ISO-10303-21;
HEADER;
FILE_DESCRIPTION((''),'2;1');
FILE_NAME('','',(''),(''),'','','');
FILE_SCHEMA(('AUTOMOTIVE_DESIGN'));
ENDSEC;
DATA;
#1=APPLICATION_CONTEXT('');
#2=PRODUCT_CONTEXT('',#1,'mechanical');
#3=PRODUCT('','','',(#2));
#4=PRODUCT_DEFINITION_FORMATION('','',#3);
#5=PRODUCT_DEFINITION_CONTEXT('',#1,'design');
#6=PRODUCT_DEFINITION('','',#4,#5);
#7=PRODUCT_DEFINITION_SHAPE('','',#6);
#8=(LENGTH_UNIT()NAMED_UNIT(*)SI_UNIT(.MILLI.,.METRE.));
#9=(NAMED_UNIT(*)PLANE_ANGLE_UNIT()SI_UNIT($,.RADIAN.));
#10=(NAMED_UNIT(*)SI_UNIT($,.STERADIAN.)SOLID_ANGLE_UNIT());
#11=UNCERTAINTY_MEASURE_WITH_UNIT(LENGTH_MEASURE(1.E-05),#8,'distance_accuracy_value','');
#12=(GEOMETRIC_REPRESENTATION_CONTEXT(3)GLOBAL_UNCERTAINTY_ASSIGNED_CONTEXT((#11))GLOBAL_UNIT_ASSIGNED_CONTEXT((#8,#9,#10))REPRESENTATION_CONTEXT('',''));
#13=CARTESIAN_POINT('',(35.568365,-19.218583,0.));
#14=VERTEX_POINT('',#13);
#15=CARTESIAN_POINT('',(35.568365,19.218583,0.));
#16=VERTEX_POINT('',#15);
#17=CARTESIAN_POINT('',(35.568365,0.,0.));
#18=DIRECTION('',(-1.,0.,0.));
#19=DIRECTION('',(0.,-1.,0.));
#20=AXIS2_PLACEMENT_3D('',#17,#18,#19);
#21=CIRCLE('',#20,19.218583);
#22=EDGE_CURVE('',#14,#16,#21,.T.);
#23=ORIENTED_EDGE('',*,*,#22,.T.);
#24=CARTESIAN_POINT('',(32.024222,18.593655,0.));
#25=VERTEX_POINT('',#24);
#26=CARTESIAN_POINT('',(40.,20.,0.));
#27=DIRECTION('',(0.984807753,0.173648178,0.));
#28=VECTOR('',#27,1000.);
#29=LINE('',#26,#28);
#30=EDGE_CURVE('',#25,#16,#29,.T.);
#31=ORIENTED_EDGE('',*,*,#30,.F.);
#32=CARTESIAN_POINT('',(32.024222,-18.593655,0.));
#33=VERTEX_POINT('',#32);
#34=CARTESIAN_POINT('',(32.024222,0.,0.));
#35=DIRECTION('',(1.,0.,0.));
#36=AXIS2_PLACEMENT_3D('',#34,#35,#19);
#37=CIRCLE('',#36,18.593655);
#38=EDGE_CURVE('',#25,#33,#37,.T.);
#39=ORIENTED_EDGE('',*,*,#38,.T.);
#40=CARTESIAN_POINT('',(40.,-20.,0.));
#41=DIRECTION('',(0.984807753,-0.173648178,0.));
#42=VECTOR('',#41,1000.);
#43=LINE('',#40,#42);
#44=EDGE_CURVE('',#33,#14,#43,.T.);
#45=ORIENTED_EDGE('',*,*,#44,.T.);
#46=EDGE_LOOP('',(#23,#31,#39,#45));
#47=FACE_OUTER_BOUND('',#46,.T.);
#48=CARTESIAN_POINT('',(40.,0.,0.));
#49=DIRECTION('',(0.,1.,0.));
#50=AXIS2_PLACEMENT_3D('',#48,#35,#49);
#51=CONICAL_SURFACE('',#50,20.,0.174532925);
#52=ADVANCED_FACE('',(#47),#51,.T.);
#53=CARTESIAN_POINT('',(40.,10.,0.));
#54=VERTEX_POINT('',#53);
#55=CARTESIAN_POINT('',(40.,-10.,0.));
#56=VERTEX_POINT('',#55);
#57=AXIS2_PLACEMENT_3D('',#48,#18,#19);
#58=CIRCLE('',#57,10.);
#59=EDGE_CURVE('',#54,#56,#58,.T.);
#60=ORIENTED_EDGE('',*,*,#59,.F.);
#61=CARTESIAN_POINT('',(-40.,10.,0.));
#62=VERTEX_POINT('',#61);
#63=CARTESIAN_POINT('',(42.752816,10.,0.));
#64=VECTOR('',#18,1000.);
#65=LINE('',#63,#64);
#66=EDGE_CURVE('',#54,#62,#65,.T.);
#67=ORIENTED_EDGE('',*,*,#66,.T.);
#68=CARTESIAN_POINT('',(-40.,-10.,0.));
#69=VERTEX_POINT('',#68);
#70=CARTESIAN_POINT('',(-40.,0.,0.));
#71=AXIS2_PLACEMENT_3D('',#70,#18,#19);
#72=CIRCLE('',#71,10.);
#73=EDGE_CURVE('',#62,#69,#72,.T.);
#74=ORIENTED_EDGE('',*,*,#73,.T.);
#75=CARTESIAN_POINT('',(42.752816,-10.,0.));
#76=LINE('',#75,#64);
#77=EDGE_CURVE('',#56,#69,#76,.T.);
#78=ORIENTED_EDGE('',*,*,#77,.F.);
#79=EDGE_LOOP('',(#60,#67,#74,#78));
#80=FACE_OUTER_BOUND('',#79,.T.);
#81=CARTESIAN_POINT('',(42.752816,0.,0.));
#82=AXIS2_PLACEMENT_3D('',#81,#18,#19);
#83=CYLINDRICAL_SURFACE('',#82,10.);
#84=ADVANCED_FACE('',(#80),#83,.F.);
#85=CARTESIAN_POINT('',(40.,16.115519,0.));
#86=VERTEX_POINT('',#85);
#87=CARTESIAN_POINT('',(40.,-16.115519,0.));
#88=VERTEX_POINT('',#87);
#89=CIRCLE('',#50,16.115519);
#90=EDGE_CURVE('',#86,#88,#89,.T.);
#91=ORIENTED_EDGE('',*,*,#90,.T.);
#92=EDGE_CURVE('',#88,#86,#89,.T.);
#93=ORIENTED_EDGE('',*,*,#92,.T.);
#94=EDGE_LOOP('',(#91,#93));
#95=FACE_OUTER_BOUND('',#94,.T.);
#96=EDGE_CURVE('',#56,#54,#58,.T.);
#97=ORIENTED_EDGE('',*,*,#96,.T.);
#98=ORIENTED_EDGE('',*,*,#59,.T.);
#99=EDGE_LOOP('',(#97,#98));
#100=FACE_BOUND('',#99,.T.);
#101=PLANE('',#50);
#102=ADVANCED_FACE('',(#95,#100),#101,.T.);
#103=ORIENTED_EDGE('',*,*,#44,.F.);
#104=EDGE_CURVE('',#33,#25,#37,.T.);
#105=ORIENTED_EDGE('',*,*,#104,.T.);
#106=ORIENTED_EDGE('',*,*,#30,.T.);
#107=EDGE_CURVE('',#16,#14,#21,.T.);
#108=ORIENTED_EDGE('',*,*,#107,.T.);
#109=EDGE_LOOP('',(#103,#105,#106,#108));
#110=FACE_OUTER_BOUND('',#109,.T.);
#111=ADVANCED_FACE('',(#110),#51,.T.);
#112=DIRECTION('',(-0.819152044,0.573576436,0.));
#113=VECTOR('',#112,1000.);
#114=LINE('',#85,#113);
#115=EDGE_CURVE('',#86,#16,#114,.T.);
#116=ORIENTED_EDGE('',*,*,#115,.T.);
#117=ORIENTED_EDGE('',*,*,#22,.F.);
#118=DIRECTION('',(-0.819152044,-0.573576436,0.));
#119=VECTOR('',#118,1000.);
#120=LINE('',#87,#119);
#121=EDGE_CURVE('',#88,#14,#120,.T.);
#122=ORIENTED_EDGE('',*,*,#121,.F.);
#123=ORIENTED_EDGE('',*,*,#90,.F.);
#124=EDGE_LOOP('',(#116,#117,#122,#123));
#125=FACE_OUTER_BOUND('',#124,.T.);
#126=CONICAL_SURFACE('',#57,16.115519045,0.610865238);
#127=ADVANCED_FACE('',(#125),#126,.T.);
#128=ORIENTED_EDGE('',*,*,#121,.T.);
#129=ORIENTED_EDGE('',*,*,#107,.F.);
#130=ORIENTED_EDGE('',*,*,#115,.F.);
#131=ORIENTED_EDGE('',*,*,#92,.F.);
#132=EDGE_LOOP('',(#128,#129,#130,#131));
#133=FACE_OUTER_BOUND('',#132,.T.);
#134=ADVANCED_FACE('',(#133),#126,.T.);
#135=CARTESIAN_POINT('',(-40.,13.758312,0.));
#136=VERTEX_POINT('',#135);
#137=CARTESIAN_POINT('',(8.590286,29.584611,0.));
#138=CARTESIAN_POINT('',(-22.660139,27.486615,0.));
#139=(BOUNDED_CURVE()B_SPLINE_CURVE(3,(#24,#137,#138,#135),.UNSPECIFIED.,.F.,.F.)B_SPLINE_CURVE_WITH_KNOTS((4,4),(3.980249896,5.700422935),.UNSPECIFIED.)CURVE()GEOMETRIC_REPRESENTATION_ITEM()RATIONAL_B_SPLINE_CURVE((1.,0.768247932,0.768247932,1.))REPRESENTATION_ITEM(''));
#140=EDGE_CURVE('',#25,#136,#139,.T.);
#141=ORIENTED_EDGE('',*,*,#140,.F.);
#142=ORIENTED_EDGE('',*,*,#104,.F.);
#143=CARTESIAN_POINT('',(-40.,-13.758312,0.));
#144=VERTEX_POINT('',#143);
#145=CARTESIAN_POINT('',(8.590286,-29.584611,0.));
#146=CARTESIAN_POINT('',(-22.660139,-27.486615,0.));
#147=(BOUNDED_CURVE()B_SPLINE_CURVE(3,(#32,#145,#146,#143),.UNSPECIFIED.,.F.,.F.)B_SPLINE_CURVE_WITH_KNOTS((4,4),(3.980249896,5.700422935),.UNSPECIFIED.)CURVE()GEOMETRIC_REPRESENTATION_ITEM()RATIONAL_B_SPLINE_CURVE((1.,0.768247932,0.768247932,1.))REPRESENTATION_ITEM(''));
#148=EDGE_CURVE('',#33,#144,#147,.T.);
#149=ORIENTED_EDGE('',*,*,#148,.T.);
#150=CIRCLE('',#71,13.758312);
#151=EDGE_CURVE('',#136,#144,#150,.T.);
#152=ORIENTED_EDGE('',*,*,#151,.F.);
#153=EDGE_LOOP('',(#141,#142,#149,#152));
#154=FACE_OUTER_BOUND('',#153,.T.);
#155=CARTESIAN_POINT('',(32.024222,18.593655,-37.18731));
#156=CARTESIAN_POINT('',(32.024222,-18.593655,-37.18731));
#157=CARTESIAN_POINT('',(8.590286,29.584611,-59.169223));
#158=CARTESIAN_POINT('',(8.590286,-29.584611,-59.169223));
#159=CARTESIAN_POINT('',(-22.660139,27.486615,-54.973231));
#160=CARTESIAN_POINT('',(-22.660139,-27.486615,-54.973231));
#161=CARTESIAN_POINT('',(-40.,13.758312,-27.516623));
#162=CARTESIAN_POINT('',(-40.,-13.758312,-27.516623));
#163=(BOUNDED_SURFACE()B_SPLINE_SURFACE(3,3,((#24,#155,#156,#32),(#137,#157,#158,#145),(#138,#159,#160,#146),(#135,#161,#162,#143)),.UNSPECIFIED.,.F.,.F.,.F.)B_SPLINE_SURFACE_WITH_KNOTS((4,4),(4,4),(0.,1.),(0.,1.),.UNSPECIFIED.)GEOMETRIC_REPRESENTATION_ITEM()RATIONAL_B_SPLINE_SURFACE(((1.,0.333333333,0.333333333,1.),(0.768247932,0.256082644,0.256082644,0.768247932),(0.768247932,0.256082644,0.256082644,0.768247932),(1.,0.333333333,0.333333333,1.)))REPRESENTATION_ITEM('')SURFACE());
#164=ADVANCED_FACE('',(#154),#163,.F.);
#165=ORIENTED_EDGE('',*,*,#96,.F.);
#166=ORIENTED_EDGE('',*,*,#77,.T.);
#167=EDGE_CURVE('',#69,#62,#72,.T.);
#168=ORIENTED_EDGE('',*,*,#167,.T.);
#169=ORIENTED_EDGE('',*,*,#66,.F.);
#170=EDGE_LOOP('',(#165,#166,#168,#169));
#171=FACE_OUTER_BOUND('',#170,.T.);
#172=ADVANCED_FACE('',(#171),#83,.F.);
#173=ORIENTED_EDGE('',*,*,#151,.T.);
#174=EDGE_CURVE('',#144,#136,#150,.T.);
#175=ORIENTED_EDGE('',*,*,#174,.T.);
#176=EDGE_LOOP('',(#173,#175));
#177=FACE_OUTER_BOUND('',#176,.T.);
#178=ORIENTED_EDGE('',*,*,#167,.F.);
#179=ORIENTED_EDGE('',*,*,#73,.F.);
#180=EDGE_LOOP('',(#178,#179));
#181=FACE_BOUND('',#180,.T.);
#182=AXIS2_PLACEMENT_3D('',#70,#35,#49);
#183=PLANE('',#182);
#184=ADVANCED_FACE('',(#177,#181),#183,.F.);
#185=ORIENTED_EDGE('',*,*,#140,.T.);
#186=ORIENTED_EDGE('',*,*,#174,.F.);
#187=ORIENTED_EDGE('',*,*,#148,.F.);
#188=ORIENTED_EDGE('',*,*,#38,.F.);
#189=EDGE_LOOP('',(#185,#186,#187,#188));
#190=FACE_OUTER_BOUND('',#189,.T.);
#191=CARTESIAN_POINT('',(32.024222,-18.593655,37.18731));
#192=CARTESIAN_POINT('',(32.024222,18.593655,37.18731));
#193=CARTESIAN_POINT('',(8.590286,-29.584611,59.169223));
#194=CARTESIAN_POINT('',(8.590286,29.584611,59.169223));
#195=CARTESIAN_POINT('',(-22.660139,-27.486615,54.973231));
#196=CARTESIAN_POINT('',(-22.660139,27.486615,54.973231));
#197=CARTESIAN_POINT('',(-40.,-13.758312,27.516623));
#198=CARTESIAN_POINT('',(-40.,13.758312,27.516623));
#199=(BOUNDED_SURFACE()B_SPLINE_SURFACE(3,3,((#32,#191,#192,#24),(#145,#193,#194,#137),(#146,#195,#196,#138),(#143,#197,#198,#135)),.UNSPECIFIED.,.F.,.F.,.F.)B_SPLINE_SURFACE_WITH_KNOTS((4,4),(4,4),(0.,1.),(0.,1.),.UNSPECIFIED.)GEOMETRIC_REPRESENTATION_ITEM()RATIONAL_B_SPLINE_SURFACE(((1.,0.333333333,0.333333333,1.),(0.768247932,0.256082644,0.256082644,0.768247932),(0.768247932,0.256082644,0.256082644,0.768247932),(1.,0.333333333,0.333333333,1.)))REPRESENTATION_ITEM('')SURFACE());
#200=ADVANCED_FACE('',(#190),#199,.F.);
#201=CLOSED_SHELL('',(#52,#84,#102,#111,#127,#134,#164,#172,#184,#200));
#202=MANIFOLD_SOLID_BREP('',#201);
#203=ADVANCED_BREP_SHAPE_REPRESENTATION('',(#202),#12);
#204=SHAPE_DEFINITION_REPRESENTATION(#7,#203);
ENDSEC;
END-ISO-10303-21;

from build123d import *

# Parameters (mm, degrees)
SKETCH2_R           = 20
SKETCH2_R_2         = 13.75831161
BOSS_EXTRUDE2_DEPTH = 9.864364
BOSS_EXTRUDE2_DRAFT = -10
CHAMFER2_SIZE       = 4.5
CHAMFER2_SIZE2      = 3.884480955


with BuildPart() as part:
    # Sketch1 → Revolve2 (revolve)
    with BuildSketch(Plane.XY, mode=Mode.PRIVATE) as revolve2_sk:
        with BuildLine():
            Line((-40, 10), (40, 10))
            add(Edge.make_bspline(
                [(40, 10), (0, 48.4), (-40, 10)],
                knots=[0.471861837, 0.471861837, 0.471861837, 2.669730816, 2.669730816, 2.669730816], degree=2, weights=[1, 0.454545455, 1]))
        make_face()
        with BuildLine():
            Line((-40, 13.75831161), (-40, 10))
            add(Edge.make_bspline(
                [(40, 10), (0, 48.4), (-40, 10)],
                knots=[0.471861837, 0.471861837, 0.471861837, 2.669730816, 2.669730816, 2.669730816], degree=2, weights=[1, 0.454545455, 1]))
            Line((40, 10), (40, 13.75831161))
            add(Edge.make_bspline(
                [(40, 13.75831161), (25.800917492, 25), (0, 25)],
                knots=[0.582762373, 0.582762373, 0.582762373, 1.570796327, 1.570796327, 1.570796327], degree=2, weights=[1, 0.775166232, 0.775166232]))
            add(Edge.make_bspline(
                [(0, 25), (-25.800917492, 25), (-40, 13.75831161)],
                knots=[1.570796327, 1.570796327, 1.570796327, 2.558830281, 2.558830281, 2.558830281], degree=2, weights=[0.775166232, 0.775166232, 1]))
        make_face()
    revolve(revolve2_sk.sketch.rotate(Axis((42.752815742, 0, 0), (1, 0, 0)), 180), axis=Axis((42.752815742, 0, 0), (1, 0, 0)))


with BuildPart() as boss_extrude2_tool:
    # Sketch2 → Boss-Extrude2 (with draft: the straight prism first)
    with BuildSketch(Plane(origin=(40, 0, 0), x_dir=(0, 0, -1), z_dir=(1, 0, 0))):
        Circle(SKETCH2_R)
        Circle(SKETCH2_R_2, mode=Mode.SUBTRACT)
    extrude(amount=-BOSS_EXTRUDE2_DEPTH)
    # Boss-Extrude2: the draft: its side faces are tilted about the plane it starts from
    boss_extrude2_sides = [boss_extrude2_tool.faces().sort_by_distance(p)[0] for p in [
        (35.067818, 0, 20),
        (35.067818, 0, 13.75831161),
    ]]
    draft(boss_extrude2_sides, Plane(origin=(40, 0, 0), x_dir=(0, 0, -1), z_dir=(1, 0, 0)), BOSS_EXTRUDE2_DRAFT)


with BuildPart() as part_1:
    add(part.part)

    # Boss-Extrude2: add boss_extrude2_tool
    add(boss_extrude2_tool.part)

    # Chamfer2
    chamfer2_edges = [part_1.edges().sort_by_distance(p)[0] for p in [
        (40, 0, 20),
    ]]
    chamfer2_side = [part_1.faces().sort_by_distance(p)[0] for p in [
        (36.012111156, 0, 19.296827601),
    ]]
    chamfer(chamfer2_edges, length=CHAMFER2_SIZE, length2=CHAMFER2_SIZE2, reference=chamfer2_side[0])


solid = part_1.part
